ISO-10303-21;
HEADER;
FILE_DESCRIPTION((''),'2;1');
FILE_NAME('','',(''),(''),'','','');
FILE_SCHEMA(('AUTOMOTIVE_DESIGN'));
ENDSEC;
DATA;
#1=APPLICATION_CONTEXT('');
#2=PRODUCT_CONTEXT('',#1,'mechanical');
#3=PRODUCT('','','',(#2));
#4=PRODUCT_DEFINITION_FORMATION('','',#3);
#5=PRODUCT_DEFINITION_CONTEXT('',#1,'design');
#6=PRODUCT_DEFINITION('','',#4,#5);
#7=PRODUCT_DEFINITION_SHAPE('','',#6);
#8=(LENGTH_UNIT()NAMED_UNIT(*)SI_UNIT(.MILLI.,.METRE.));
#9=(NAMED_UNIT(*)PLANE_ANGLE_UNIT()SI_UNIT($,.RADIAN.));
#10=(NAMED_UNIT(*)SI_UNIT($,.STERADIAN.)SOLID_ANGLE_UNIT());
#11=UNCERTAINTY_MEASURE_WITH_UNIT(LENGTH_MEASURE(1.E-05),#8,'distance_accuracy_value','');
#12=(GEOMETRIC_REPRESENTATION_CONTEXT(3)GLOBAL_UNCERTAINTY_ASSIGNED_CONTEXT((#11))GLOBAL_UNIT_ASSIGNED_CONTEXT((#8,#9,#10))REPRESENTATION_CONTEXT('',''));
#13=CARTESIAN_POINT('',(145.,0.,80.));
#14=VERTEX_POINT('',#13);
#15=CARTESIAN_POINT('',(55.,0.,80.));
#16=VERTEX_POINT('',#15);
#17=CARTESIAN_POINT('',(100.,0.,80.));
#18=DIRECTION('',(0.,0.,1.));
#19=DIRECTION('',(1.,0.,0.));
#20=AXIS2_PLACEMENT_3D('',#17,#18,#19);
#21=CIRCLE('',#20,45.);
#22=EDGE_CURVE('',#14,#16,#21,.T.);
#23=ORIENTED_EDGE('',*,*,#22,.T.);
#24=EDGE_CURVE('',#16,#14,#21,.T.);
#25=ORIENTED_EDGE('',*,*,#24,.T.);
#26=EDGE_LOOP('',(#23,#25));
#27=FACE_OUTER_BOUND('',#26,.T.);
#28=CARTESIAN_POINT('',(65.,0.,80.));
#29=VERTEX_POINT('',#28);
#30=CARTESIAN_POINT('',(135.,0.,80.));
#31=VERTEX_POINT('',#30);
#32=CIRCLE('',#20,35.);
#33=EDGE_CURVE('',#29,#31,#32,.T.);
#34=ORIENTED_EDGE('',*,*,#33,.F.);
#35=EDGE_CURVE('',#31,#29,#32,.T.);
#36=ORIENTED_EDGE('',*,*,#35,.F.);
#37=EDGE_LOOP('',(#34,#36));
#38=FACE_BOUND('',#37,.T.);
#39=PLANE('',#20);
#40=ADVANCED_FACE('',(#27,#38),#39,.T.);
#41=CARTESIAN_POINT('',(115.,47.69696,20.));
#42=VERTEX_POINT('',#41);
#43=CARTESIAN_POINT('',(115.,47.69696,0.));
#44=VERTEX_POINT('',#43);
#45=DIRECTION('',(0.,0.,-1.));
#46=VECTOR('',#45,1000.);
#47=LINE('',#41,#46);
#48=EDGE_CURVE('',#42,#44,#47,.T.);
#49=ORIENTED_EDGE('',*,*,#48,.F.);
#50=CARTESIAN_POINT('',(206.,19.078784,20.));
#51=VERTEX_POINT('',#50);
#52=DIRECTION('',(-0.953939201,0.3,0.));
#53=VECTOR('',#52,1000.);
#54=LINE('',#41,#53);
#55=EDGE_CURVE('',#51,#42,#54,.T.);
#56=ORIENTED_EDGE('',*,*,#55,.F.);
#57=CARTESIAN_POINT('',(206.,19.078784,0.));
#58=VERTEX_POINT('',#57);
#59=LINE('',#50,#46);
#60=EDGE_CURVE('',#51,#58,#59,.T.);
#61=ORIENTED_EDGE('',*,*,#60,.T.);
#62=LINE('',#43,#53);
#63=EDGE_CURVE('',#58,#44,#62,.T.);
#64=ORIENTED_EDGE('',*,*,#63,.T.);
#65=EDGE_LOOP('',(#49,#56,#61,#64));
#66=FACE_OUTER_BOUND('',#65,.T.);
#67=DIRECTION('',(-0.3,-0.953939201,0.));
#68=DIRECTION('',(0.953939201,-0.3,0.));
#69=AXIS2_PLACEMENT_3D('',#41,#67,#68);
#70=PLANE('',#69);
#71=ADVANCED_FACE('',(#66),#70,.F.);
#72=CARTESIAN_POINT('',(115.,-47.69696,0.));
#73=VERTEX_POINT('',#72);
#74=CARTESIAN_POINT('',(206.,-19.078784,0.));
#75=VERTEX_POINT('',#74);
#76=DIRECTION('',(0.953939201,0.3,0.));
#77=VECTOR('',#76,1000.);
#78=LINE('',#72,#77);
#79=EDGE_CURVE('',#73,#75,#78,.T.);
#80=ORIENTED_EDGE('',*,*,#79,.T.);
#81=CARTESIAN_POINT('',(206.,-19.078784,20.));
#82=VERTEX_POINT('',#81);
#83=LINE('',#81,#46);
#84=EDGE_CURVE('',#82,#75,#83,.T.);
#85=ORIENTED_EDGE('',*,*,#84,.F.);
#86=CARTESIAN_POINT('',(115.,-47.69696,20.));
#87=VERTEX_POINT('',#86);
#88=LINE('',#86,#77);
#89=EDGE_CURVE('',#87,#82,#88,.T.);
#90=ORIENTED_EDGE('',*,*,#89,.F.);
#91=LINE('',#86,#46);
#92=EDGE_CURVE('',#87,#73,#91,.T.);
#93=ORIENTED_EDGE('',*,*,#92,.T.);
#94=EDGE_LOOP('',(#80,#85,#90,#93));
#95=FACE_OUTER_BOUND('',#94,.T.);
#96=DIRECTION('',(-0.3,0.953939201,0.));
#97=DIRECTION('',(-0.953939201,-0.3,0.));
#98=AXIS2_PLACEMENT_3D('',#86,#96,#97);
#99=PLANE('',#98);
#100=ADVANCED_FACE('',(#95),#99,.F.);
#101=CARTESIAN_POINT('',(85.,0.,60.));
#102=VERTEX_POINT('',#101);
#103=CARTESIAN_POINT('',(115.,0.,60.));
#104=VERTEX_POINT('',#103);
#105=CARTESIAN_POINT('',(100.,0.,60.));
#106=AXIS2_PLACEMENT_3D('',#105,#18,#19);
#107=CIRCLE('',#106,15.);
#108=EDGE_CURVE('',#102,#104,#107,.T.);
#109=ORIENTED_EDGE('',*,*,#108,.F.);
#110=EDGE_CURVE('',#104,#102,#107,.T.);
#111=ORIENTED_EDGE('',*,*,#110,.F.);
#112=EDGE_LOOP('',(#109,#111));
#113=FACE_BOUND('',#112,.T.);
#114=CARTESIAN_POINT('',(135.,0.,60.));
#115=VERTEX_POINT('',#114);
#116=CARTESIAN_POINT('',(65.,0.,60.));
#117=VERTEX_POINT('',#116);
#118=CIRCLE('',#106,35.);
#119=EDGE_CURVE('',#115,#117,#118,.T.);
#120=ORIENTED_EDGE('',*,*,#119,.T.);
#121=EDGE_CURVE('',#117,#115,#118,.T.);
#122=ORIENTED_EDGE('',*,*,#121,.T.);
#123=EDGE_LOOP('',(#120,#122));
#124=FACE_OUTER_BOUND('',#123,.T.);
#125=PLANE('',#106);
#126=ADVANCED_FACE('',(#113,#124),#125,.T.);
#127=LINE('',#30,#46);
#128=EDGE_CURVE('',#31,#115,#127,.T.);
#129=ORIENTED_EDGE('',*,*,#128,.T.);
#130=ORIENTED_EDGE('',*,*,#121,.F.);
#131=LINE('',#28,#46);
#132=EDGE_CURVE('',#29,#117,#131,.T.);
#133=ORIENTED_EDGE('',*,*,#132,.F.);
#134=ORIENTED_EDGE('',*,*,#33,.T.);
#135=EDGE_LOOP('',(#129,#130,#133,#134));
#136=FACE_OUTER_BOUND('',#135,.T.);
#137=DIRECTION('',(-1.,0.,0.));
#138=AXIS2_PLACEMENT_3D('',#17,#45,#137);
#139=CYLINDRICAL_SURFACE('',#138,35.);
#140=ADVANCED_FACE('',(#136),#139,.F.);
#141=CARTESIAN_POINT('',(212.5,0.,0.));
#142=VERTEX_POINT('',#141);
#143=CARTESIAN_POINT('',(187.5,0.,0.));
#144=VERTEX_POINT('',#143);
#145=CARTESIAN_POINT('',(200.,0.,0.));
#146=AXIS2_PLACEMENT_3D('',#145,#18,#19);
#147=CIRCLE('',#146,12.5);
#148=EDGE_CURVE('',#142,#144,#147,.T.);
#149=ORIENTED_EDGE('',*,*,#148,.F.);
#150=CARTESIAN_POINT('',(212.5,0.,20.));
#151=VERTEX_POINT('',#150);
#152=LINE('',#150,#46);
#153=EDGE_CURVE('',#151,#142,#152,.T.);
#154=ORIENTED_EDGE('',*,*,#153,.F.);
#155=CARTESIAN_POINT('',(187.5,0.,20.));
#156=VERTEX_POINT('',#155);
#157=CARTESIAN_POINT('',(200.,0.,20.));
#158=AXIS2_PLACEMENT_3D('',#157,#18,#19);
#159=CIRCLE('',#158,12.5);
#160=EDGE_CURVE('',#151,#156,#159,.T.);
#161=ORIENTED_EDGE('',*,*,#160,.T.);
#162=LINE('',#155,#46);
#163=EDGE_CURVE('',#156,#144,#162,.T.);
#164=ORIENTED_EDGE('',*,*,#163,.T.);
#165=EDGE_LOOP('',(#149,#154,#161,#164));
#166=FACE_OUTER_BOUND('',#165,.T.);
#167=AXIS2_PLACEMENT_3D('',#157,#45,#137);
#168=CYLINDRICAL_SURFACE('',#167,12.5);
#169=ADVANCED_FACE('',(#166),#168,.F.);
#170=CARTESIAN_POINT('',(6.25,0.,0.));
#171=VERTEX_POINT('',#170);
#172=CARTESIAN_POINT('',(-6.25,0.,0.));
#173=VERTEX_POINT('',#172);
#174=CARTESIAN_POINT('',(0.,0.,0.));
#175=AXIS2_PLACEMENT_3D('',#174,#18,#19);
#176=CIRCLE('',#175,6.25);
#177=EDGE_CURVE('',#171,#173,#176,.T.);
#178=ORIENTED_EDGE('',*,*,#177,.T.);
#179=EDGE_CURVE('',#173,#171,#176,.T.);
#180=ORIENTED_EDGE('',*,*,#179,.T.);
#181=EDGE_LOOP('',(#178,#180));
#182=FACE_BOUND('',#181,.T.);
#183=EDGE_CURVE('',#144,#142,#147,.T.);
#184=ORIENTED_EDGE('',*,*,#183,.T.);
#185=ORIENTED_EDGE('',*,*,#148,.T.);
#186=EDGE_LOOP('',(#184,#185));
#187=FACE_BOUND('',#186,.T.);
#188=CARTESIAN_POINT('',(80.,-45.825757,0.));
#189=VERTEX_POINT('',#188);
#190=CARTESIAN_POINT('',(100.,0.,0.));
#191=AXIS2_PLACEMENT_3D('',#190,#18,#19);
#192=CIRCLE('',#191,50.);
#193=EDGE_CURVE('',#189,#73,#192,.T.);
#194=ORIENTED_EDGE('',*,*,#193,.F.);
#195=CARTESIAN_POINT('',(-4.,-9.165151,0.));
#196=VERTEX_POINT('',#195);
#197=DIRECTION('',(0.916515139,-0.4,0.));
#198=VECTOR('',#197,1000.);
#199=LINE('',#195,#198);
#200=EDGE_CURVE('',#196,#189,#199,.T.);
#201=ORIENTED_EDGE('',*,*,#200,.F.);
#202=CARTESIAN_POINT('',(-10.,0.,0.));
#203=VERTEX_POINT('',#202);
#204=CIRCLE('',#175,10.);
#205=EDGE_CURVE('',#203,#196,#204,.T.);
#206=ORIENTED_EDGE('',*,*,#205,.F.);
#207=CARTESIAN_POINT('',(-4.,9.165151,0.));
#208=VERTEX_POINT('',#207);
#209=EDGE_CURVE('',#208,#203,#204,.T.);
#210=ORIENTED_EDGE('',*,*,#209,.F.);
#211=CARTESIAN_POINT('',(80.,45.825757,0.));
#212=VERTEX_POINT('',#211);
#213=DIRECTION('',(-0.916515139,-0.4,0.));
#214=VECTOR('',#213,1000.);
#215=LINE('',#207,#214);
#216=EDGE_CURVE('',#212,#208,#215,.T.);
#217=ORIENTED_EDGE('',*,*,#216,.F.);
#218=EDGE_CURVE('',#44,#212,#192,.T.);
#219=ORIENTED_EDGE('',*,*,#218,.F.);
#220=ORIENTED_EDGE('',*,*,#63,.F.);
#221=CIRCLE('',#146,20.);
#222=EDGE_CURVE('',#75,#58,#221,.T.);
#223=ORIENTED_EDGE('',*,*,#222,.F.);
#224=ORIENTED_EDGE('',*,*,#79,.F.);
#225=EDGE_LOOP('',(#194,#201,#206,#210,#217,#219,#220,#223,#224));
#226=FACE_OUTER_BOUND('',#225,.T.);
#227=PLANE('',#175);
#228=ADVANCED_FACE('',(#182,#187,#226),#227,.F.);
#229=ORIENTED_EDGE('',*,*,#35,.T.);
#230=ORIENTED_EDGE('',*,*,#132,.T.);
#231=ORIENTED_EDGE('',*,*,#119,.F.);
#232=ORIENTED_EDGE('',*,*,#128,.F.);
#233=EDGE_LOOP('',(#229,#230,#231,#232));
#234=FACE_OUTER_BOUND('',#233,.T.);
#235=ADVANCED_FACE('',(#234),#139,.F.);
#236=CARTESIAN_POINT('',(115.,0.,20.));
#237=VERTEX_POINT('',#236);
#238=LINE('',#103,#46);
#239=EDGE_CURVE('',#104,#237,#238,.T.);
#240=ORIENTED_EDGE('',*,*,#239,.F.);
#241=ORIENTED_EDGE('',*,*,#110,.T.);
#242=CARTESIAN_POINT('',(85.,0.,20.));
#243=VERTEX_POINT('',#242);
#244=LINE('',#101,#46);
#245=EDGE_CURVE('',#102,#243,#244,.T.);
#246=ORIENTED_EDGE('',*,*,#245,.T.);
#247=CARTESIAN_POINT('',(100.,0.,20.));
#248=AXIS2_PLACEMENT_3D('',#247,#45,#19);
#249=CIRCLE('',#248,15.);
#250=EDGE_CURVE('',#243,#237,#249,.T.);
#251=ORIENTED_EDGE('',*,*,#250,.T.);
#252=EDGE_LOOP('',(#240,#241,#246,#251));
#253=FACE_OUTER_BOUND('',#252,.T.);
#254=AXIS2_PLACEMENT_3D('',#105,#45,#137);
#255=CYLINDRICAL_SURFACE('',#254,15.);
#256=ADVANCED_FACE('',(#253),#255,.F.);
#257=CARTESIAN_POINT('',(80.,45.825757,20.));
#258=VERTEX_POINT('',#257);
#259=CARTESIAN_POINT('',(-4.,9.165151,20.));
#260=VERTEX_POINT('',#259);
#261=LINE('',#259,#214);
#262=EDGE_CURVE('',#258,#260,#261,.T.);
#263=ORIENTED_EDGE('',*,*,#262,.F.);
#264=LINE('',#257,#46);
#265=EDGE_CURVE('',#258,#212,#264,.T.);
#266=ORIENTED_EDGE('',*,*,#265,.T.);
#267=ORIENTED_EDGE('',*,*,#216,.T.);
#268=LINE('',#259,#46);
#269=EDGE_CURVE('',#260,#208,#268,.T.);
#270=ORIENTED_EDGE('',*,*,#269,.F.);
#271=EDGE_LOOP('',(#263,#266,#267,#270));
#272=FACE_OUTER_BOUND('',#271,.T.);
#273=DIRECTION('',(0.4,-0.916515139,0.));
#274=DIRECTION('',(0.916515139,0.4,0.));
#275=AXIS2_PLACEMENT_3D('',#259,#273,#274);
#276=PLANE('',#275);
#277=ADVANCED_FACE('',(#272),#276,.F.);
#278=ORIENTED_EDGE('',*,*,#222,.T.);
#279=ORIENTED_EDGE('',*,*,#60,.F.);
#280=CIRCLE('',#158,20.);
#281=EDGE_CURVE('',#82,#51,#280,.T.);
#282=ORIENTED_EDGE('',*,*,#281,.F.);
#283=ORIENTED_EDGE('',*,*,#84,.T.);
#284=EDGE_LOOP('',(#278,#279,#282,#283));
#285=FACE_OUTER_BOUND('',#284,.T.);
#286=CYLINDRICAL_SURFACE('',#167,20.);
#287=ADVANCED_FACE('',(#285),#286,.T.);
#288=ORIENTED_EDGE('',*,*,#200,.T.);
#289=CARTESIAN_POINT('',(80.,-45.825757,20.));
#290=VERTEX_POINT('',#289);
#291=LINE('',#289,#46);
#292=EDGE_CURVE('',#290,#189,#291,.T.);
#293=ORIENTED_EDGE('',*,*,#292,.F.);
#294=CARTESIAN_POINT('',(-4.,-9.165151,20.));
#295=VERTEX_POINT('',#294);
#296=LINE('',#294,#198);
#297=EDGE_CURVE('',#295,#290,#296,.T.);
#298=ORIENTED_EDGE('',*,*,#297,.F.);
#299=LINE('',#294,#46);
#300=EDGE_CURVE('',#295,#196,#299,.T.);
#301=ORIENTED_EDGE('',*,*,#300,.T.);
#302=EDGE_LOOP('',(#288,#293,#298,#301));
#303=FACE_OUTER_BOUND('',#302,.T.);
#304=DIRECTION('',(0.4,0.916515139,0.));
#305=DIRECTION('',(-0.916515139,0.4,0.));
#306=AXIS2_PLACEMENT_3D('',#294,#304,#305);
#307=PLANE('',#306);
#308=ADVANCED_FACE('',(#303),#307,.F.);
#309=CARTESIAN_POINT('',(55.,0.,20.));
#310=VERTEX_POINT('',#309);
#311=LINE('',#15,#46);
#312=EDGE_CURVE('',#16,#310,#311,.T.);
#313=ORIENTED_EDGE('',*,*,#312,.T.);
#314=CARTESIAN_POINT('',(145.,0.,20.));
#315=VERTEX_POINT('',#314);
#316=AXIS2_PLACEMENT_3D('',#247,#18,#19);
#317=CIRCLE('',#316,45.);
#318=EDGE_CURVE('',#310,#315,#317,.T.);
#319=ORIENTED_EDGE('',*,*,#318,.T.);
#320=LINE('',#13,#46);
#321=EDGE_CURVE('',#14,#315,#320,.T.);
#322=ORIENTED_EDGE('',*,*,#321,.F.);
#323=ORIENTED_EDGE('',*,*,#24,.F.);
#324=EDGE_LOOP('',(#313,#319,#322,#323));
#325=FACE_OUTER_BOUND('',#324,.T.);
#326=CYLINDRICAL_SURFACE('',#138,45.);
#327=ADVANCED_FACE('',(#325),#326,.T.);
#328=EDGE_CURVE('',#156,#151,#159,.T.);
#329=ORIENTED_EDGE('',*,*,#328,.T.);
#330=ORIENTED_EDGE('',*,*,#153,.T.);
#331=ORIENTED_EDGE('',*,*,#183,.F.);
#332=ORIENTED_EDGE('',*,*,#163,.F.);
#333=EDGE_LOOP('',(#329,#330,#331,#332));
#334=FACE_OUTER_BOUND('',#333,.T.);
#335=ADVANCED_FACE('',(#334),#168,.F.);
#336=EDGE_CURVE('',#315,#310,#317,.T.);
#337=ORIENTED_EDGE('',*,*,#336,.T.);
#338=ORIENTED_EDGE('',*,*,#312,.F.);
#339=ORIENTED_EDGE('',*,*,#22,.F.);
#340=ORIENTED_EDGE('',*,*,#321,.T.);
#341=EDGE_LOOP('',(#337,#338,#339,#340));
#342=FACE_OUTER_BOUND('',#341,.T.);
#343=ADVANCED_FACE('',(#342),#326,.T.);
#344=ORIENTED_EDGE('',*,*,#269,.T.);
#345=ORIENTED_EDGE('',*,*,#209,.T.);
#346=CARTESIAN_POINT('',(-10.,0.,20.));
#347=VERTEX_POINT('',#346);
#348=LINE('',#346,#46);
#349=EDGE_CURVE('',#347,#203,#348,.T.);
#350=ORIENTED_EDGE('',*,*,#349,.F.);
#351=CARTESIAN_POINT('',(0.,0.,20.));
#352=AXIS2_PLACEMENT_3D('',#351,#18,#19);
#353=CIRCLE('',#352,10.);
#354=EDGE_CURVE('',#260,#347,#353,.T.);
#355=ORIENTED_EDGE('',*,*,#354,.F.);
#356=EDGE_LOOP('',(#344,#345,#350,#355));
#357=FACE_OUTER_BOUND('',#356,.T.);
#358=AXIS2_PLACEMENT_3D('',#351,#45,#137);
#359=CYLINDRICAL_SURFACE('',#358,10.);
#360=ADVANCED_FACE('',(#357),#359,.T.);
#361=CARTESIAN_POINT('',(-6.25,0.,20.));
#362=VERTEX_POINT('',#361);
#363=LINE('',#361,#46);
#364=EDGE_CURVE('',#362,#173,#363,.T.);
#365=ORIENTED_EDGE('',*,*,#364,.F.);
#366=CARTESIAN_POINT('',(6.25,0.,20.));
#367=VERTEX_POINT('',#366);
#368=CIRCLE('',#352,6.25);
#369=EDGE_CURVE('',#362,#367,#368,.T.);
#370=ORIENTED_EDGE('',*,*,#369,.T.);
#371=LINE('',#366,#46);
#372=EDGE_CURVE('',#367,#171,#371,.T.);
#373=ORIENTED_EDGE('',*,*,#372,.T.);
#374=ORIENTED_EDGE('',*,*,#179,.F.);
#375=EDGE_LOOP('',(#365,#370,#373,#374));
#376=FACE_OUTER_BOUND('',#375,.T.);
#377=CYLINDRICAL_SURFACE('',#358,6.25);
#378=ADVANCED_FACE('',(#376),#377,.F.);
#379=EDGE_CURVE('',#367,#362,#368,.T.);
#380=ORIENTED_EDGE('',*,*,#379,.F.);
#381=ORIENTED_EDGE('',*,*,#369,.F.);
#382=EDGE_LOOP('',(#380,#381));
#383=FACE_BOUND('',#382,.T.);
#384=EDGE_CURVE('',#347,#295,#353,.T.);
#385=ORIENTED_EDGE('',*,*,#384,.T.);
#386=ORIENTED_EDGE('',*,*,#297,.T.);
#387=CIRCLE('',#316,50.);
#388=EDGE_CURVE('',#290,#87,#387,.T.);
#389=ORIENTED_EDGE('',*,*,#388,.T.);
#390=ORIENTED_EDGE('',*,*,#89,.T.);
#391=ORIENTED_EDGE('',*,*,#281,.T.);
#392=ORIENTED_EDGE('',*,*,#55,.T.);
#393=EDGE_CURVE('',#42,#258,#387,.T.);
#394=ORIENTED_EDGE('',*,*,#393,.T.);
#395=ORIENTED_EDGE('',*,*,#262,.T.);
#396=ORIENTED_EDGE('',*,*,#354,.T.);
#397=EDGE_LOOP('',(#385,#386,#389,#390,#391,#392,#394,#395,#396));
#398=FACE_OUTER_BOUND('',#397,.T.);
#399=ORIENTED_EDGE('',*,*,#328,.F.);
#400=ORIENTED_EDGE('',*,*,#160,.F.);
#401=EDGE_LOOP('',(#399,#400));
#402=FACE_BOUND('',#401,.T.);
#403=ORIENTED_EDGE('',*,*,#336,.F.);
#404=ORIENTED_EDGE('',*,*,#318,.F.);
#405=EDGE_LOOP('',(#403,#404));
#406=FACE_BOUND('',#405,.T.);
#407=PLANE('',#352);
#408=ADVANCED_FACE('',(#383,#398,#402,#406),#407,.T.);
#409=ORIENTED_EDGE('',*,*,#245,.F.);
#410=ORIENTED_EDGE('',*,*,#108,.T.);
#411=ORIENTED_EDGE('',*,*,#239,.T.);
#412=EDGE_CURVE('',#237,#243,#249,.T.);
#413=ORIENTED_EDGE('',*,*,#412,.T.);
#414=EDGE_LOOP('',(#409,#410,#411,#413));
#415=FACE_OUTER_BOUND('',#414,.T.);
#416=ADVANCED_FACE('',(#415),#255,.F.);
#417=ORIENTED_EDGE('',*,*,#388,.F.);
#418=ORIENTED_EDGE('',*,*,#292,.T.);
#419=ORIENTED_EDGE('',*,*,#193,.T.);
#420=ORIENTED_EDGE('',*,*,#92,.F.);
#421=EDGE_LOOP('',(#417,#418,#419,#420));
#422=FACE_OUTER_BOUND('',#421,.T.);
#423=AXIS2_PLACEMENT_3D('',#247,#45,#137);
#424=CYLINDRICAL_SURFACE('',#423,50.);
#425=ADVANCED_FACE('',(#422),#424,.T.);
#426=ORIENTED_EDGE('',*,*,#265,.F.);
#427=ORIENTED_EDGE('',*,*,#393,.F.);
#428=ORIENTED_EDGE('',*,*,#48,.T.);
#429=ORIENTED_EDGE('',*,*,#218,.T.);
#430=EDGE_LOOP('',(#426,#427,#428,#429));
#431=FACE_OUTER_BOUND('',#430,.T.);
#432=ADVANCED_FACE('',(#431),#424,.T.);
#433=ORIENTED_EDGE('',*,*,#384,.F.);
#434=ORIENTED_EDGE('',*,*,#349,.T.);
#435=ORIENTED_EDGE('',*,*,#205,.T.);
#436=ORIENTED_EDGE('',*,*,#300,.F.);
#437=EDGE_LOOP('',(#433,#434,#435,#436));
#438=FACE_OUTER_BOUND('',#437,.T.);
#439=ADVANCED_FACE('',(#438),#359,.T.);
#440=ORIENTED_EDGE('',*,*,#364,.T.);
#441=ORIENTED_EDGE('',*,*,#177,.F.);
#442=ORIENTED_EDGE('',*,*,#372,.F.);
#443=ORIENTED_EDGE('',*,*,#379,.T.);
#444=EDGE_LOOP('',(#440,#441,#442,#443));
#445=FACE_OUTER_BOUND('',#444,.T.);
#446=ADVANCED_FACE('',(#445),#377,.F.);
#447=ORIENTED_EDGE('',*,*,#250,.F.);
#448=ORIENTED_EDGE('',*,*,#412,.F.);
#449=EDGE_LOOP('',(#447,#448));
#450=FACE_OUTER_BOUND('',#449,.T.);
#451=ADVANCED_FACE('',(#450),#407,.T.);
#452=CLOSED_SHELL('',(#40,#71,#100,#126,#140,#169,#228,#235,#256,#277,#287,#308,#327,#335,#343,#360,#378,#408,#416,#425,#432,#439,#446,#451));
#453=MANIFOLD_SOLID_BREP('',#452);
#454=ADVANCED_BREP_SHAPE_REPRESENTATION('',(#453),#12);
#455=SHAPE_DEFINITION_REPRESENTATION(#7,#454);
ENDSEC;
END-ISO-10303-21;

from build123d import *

# Parameters (mm, degrees)
FLANGE_PLATE_PROFILE_R       = 6.25
FLANGE_PLATE_PROFILE_R_2     = 12.5
FLANGE_PLATE_20MM_DEPTH      = 20
HUB_PROFILE_90_70_R          = 45
HUB_PROFILE_90_70_R_2        = 35
HUB_90X60_DEPTH              = 60
INNER_BOSS_PROFILE_70_30_R   = 35
INNER_BOSS_PROFILE_70_30_R_2 = 15
INNER_BOSS_70_BORE_30_DEPTH  = 40


with BuildPart() as part:
    # Flange Plate Profile → Flange Plate 20mm (new body)
    with BuildSketch(Plane.XY):
        with BuildLine():
            Line((-4, 9.16515139), (80, 45.82575695))
            ThreePointArc((80, 45.82575695), (97.330664824, 49.928695654), (115, 47.696960071))
            Line((115, 47.696960071), (206, 19.078784028))
            ThreePointArc((206, 19.078784028), (220, 0), (206, -19.078784028))
            Line((206, -19.078784028), (115, -47.696960071))
            ThreePointArc((115, -47.696960071), (97.330664824, -49.928695654), (80, -45.82575695))
            Line((80, -45.82575695), (-4, -9.16515139))
            ThreePointArc((-4, -9.16515139), (-10, 0), (-4, 9.16515139))
        make_face()
        Circle(FLANGE_PLATE_PROFILE_R, mode=Mode.SUBTRACT)
        with Locations((200, 0)):
            Circle(FLANGE_PLATE_PROFILE_R_2, mode=Mode.SUBTRACT)
    extrude(amount=FLANGE_PLATE_20MM_DEPTH)

    # Hub Profile Ø90-Ø70 → Hub Ø90x60 (add)
    with BuildSketch(Plane.XY.offset(20)):
        with Locations((100, 0)):
            Circle(HUB_PROFILE_90_70_R)
        with Locations((100, 0)):
            Circle(HUB_PROFILE_90_70_R_2, mode=Mode.SUBTRACT)
    extrude(amount=HUB_90X60_DEPTH)

    # Inner Boss Profile Ø70-Ø30 → Inner Boss Ø70 Bore Ø30 (add)
    with BuildSketch(Plane.XY.offset(20)):
        with Locations((100, 0)):
            Circle(INNER_BOSS_PROFILE_70_30_R)
        with Locations((100, 0)):
            Circle(INNER_BOSS_PROFILE_70_30_R_2, mode=Mode.SUBTRACT)
    extrude(amount=INNER_BOSS_70_BORE_30_DEPTH)


solid = part.part
